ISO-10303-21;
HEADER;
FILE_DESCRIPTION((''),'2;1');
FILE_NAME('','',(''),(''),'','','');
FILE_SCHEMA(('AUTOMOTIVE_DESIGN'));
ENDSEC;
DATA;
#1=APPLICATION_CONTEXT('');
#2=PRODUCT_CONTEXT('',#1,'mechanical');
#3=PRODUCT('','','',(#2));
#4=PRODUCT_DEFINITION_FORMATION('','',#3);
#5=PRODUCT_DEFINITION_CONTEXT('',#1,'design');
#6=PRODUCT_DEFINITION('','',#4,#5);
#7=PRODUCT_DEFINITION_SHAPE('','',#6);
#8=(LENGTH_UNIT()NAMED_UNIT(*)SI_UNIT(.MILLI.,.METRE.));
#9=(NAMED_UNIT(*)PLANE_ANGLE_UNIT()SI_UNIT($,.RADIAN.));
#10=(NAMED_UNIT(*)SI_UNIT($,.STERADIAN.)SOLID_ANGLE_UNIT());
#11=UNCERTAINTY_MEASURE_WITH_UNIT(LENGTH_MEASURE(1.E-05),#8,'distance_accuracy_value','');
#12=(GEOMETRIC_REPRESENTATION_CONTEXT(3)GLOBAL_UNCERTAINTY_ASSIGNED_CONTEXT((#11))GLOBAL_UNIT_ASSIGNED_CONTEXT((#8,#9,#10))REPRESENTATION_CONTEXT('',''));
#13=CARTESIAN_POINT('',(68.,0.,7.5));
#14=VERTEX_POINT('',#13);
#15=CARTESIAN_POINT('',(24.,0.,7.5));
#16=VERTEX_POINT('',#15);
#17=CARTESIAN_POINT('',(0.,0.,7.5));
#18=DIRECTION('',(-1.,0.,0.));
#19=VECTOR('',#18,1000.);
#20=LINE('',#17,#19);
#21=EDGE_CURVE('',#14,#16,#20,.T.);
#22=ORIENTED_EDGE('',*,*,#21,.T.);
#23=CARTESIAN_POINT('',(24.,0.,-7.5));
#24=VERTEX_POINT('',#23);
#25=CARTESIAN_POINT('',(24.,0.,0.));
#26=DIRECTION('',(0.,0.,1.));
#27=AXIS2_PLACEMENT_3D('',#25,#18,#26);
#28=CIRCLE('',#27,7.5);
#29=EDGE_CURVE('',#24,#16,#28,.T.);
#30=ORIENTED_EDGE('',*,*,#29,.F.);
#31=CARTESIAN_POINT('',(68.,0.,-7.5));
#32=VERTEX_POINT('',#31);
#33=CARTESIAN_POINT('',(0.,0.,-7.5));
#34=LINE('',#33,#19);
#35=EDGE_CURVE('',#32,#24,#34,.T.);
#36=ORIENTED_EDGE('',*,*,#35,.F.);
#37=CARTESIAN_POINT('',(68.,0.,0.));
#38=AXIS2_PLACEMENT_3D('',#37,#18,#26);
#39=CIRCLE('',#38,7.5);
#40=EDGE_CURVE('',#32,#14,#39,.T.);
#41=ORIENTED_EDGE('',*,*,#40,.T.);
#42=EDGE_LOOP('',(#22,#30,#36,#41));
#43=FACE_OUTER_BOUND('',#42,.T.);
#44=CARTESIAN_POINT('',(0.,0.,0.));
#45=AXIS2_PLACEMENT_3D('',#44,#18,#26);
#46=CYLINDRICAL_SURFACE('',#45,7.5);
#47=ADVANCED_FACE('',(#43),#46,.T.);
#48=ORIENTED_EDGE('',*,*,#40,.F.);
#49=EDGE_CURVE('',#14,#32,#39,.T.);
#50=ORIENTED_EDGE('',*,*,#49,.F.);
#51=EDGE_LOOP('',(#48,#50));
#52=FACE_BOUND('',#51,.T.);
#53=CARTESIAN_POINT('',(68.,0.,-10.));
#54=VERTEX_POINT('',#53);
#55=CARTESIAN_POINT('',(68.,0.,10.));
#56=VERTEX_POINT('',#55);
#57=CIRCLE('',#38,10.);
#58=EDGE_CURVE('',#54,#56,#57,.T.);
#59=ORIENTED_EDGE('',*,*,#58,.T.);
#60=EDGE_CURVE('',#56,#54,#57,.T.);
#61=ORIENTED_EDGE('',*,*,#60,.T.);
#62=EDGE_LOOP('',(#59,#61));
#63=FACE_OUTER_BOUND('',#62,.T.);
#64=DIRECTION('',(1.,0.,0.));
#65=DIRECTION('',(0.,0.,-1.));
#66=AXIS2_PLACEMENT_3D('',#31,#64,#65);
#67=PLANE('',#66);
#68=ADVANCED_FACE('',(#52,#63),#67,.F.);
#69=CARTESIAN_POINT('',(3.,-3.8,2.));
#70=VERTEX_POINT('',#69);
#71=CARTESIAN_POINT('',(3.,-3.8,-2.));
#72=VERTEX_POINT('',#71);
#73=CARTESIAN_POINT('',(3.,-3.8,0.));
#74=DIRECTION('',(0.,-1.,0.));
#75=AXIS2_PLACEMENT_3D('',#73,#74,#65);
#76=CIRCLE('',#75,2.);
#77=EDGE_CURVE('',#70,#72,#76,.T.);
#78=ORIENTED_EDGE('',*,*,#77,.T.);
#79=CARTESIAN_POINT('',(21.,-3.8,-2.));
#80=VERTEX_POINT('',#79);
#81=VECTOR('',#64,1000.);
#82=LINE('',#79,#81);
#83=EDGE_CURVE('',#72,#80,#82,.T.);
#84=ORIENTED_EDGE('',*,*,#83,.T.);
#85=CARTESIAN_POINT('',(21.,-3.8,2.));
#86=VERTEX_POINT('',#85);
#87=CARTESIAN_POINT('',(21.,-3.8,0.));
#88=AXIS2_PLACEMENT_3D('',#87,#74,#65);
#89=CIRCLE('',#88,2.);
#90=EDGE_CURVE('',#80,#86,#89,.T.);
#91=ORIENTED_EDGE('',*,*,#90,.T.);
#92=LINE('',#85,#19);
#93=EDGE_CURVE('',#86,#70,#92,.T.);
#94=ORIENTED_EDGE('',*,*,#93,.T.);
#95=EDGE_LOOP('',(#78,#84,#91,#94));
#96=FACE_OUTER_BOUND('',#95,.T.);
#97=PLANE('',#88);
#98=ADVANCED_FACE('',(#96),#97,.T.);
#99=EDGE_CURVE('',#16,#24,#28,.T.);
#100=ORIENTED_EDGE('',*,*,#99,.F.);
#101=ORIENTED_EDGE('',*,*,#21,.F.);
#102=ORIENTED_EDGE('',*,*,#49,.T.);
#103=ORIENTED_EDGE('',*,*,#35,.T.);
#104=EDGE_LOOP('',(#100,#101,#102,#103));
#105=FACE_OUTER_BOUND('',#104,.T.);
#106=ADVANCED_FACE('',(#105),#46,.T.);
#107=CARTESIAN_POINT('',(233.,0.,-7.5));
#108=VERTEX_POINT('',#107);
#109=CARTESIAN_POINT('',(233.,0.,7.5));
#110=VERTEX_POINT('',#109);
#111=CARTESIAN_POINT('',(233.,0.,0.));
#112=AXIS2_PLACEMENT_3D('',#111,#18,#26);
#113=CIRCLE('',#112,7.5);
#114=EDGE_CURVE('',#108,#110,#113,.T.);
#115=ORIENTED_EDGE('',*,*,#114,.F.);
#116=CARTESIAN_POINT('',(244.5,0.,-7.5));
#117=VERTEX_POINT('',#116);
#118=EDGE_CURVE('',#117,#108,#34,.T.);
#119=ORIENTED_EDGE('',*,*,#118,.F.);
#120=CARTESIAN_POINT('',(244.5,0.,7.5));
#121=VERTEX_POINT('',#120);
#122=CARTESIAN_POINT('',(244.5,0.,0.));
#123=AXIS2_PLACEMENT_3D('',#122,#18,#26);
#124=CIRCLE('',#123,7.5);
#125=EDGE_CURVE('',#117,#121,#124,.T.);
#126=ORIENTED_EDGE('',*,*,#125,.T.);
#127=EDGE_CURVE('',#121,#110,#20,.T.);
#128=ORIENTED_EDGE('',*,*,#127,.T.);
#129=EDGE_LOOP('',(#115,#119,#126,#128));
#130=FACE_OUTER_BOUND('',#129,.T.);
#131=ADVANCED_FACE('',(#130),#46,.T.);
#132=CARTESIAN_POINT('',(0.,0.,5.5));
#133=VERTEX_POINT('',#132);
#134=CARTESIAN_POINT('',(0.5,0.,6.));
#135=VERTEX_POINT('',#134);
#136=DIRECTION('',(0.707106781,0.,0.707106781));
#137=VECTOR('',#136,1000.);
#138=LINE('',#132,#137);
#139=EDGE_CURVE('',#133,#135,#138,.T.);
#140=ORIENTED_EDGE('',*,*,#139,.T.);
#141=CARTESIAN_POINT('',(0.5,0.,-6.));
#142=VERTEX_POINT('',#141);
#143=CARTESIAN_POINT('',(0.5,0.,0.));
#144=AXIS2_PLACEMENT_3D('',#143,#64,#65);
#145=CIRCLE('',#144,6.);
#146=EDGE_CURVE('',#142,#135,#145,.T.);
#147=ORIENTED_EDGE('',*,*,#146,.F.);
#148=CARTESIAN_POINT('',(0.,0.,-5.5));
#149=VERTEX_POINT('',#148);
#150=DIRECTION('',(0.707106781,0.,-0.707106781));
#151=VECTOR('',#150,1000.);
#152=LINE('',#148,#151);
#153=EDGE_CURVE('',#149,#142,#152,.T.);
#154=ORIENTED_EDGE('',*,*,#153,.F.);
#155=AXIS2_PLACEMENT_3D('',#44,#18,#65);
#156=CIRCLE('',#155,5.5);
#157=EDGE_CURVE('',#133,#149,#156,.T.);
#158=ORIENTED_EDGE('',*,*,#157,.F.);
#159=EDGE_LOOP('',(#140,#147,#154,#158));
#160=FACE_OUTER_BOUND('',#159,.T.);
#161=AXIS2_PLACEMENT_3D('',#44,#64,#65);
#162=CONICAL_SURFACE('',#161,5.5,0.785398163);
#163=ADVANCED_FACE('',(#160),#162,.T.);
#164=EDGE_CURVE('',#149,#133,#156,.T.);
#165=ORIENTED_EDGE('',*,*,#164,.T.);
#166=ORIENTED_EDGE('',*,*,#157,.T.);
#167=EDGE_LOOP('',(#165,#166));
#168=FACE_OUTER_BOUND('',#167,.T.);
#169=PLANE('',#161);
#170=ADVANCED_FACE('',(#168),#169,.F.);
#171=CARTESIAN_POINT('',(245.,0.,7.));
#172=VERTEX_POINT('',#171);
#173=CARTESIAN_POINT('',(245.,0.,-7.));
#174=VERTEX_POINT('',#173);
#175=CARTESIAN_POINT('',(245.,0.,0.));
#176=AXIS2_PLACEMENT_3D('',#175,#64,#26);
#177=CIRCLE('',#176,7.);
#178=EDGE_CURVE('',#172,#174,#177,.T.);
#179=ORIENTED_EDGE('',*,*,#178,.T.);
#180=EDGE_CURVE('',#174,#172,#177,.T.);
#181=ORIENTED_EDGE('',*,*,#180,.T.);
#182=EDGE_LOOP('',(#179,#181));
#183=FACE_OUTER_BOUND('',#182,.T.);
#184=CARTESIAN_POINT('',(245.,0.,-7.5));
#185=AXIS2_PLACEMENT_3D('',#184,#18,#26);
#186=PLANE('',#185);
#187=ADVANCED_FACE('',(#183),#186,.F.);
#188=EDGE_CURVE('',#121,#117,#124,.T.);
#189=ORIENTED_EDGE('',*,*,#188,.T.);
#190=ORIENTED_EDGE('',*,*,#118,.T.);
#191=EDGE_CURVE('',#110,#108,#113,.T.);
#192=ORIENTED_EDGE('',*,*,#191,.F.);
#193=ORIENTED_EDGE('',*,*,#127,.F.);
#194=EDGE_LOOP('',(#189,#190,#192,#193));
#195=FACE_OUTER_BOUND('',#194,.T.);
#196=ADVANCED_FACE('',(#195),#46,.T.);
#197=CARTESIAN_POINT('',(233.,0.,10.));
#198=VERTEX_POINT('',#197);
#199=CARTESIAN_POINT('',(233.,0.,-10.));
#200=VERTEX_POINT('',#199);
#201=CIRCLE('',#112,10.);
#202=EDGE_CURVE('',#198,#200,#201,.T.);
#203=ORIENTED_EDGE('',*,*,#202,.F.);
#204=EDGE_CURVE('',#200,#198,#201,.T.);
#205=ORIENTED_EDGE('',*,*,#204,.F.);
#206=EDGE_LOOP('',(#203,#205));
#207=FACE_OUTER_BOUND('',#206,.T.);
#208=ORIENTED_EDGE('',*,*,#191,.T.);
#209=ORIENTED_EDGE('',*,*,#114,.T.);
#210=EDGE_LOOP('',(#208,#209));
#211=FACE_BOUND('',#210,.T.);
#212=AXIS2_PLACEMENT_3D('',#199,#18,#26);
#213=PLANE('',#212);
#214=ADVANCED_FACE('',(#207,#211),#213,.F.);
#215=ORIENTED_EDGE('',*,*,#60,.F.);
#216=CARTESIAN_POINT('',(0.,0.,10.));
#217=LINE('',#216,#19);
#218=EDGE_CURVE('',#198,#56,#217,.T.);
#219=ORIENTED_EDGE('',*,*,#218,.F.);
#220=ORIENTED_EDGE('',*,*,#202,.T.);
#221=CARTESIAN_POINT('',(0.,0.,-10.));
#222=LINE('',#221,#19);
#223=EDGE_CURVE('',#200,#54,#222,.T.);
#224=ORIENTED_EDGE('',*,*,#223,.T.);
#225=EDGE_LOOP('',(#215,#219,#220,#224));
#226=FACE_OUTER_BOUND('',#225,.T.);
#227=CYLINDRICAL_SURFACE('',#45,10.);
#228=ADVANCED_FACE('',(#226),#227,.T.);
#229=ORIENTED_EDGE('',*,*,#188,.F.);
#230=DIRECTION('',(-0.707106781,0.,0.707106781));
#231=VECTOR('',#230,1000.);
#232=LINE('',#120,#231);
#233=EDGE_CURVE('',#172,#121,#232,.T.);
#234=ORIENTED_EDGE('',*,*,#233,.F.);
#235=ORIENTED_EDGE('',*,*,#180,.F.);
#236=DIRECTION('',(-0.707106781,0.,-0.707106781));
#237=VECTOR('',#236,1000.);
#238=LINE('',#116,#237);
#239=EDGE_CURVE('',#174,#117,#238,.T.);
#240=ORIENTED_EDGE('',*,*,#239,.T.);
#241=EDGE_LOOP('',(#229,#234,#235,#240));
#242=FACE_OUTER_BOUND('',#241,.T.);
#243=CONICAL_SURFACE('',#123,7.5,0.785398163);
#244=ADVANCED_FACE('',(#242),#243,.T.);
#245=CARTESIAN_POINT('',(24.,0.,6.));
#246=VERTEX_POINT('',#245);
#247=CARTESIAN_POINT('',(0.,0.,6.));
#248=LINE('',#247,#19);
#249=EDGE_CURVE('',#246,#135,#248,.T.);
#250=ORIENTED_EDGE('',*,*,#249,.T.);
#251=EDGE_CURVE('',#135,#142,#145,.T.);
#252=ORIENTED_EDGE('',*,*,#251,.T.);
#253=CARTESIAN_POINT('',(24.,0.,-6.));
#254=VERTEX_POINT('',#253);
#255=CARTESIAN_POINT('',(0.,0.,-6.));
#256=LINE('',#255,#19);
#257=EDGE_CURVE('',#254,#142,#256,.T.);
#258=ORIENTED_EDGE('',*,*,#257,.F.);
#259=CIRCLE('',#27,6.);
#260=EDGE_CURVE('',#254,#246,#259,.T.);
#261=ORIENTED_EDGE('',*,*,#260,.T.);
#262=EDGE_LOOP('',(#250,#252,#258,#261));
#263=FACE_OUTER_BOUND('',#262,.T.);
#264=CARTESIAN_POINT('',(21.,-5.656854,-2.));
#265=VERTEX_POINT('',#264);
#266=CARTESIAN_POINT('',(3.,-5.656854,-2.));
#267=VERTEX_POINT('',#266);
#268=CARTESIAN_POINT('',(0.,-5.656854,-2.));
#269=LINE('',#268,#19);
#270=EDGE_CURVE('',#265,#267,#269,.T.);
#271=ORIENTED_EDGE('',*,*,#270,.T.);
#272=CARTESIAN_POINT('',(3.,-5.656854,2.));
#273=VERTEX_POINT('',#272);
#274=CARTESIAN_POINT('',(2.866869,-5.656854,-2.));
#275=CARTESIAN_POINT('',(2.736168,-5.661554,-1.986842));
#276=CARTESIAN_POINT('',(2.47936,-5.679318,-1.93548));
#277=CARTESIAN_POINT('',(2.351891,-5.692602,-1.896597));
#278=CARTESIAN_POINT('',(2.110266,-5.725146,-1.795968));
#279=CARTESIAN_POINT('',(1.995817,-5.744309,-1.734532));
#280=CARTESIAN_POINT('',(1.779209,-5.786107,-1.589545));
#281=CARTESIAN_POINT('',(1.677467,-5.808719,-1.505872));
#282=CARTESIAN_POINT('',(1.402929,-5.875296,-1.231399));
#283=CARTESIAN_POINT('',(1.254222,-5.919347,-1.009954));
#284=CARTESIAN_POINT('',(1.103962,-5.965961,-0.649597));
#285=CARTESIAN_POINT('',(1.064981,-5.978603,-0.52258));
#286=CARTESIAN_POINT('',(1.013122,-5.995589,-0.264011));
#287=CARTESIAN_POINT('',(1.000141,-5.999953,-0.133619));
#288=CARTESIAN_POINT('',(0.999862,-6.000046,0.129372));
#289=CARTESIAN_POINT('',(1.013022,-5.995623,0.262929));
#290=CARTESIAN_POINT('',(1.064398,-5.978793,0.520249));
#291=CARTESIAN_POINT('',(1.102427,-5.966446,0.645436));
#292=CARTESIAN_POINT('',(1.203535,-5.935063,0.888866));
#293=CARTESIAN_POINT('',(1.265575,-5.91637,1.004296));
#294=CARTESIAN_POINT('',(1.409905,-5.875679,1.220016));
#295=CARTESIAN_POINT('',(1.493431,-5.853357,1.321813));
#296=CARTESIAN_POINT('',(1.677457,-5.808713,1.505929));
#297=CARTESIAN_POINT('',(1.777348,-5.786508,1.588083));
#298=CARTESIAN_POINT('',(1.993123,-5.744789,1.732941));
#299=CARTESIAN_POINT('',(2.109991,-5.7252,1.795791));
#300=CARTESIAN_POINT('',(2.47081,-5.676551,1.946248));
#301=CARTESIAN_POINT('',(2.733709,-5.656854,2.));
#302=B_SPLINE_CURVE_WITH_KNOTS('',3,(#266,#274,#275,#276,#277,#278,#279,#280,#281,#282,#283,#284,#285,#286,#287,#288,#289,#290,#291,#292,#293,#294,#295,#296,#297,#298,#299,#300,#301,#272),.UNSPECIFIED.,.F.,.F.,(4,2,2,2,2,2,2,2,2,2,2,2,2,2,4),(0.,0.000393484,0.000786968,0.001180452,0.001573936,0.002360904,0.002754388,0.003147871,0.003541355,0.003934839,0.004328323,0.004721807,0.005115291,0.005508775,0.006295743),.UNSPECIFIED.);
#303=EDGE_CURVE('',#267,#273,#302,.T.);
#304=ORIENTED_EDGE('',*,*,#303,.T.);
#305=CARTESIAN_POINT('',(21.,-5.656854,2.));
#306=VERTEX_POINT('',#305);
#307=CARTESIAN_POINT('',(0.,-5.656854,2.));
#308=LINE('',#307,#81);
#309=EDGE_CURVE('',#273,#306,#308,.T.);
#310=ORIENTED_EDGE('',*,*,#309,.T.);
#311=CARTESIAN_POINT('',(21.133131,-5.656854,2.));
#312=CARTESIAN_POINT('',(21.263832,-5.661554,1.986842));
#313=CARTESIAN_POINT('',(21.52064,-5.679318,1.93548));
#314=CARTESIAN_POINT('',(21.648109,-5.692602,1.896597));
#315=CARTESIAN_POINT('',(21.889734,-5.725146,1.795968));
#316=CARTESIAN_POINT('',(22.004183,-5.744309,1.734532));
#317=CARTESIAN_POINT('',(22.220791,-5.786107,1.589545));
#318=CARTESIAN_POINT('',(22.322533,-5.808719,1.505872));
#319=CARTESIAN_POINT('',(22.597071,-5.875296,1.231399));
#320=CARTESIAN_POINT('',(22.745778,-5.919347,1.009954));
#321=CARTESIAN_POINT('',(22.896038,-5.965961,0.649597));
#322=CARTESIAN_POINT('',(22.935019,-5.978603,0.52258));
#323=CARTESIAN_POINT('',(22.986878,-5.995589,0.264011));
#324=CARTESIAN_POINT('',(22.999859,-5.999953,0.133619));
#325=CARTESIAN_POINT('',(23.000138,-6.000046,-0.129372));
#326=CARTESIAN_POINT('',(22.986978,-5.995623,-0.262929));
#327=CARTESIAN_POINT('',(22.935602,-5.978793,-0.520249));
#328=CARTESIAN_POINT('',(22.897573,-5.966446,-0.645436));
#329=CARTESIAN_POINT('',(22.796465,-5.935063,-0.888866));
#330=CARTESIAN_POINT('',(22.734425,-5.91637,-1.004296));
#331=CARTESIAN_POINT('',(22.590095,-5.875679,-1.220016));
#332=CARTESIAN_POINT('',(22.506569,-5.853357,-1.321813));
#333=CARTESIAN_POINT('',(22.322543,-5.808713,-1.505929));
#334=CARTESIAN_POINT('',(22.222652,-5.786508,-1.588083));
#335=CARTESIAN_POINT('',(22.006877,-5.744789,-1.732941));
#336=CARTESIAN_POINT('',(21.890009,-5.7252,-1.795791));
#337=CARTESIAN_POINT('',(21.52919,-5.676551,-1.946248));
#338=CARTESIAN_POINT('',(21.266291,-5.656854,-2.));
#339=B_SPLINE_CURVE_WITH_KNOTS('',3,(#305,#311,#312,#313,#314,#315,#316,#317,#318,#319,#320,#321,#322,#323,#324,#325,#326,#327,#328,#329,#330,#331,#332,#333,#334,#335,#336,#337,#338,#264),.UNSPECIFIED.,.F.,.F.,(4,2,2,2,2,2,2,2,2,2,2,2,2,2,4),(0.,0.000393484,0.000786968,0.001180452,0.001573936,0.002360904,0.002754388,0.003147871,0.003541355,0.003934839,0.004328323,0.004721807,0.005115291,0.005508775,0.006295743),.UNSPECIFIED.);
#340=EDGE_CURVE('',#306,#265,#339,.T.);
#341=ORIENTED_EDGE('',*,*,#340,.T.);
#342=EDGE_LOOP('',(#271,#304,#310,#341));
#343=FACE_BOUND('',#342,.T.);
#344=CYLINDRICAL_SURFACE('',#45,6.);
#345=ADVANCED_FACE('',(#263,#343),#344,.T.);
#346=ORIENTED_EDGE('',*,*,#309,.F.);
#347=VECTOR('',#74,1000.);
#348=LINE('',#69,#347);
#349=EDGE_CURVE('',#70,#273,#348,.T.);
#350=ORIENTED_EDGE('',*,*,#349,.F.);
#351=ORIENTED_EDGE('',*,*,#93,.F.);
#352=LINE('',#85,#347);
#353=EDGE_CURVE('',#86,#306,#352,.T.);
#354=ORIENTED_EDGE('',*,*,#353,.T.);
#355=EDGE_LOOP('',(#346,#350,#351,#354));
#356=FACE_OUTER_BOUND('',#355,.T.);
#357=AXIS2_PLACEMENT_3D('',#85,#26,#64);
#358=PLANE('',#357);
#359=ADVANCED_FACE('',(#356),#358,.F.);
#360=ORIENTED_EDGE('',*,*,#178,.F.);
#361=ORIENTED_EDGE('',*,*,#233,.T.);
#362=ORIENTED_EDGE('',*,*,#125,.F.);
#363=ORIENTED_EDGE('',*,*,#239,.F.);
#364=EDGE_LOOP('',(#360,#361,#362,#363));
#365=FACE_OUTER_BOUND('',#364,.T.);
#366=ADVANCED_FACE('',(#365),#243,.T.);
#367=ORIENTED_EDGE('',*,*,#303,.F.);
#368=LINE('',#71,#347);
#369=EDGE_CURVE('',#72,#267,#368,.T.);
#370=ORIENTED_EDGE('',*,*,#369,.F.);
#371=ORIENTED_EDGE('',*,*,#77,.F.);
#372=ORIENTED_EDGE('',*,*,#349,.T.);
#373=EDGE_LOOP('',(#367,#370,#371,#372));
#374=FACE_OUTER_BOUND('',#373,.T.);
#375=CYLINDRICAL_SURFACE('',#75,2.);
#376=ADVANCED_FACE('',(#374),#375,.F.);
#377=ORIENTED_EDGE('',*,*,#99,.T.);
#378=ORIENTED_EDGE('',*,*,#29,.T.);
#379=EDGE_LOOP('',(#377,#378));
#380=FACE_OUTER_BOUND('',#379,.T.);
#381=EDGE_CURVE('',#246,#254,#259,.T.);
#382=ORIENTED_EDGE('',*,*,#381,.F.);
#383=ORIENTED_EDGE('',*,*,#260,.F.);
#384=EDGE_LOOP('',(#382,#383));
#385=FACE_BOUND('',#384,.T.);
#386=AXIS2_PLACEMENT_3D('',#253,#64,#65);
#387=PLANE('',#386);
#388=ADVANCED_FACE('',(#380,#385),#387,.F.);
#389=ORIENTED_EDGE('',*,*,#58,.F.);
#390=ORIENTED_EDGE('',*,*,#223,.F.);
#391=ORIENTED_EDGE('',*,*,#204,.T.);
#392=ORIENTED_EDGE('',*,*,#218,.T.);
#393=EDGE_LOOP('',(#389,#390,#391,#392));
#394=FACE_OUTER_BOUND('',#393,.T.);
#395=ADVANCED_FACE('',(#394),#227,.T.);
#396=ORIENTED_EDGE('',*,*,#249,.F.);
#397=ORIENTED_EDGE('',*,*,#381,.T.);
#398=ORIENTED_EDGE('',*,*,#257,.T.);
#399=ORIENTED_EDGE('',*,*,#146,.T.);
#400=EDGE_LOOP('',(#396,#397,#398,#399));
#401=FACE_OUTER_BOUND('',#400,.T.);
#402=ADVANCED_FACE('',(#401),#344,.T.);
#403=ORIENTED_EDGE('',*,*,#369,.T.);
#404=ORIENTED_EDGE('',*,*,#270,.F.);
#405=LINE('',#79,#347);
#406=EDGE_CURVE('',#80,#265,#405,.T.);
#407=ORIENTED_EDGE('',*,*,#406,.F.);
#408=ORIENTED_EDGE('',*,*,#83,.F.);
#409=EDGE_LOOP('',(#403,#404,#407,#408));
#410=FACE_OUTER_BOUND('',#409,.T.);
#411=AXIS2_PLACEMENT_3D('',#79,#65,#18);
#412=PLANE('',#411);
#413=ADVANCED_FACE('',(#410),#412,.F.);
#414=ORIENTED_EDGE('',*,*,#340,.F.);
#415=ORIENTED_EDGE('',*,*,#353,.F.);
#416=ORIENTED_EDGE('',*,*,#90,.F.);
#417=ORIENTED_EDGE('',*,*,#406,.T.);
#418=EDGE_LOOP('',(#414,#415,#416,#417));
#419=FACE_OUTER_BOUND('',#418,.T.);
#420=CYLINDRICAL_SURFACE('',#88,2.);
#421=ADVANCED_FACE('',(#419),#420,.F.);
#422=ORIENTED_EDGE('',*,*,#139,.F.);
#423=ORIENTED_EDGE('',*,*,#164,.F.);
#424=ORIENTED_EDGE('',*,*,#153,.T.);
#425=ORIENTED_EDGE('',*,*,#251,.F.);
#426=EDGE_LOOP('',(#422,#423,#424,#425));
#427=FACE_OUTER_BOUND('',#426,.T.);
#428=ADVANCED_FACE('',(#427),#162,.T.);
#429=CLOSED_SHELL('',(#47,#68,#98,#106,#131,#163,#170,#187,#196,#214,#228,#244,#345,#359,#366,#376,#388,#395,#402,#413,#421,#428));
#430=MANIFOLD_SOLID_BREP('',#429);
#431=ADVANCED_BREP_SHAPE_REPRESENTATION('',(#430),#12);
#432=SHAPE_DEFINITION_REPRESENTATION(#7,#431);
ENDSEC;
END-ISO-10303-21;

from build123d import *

# Parameters (mm, degrees)
CUT_EXTRUDE_1_DEPTH = 2.2
CHAMFER_1_SIZE      = 0.5


with BuildPart() as part:
    # 草图1 → 旋转1 (revolve)
    with BuildSketch(Plane(origin=(0, 0, 0), x_dir=(1, 0, 0), z_dir=(0, 1, 0)), mode=Mode.PRIVATE) as revolve_1_sk:
        Polygon((0, 0), (0, 6), (24, 6), (24, 7.5), (68, 7.5), (68, 10), (233, 10), (233, 7.5), (245, 7.5), (245, 0), align=None)
    revolve(revolve_1_sk.sketch.rotate(Axis((0, 0, 0), (1, 0, 0)), 180), axis=Axis((0, 0, 0), (1, 0, 0)))

    # 草图2 → 切除-拉伸1 (cut)
    with BuildSketch(Plane(origin=(0, -6, 0), x_dir=(-1, 0, 0), z_dir=(0, -1, 0))):
        with BuildLine():
            Line((-21, 2), (-3, 2))
            ThreePointArc((-3, 2), (-1, 0), (-3, -2))
            Line((-3, -2), (-21, -2))
            ThreePointArc((-21, -2), (-23, 0), (-21, 2))
        make_face()
    extrude(amount=-CUT_EXTRUDE_1_DEPTH, mode=Mode.SUBTRACT)

    # 倒角1
    chamfer_1_edges = [part.edges().sort_by_distance(p)[0] for p in [
        (0, 0, -6),
        (245, 0, -7.5),
    ]]
    chamfer(chamfer_1_edges, length=CHAMFER_1_SIZE)


solid = part.part
